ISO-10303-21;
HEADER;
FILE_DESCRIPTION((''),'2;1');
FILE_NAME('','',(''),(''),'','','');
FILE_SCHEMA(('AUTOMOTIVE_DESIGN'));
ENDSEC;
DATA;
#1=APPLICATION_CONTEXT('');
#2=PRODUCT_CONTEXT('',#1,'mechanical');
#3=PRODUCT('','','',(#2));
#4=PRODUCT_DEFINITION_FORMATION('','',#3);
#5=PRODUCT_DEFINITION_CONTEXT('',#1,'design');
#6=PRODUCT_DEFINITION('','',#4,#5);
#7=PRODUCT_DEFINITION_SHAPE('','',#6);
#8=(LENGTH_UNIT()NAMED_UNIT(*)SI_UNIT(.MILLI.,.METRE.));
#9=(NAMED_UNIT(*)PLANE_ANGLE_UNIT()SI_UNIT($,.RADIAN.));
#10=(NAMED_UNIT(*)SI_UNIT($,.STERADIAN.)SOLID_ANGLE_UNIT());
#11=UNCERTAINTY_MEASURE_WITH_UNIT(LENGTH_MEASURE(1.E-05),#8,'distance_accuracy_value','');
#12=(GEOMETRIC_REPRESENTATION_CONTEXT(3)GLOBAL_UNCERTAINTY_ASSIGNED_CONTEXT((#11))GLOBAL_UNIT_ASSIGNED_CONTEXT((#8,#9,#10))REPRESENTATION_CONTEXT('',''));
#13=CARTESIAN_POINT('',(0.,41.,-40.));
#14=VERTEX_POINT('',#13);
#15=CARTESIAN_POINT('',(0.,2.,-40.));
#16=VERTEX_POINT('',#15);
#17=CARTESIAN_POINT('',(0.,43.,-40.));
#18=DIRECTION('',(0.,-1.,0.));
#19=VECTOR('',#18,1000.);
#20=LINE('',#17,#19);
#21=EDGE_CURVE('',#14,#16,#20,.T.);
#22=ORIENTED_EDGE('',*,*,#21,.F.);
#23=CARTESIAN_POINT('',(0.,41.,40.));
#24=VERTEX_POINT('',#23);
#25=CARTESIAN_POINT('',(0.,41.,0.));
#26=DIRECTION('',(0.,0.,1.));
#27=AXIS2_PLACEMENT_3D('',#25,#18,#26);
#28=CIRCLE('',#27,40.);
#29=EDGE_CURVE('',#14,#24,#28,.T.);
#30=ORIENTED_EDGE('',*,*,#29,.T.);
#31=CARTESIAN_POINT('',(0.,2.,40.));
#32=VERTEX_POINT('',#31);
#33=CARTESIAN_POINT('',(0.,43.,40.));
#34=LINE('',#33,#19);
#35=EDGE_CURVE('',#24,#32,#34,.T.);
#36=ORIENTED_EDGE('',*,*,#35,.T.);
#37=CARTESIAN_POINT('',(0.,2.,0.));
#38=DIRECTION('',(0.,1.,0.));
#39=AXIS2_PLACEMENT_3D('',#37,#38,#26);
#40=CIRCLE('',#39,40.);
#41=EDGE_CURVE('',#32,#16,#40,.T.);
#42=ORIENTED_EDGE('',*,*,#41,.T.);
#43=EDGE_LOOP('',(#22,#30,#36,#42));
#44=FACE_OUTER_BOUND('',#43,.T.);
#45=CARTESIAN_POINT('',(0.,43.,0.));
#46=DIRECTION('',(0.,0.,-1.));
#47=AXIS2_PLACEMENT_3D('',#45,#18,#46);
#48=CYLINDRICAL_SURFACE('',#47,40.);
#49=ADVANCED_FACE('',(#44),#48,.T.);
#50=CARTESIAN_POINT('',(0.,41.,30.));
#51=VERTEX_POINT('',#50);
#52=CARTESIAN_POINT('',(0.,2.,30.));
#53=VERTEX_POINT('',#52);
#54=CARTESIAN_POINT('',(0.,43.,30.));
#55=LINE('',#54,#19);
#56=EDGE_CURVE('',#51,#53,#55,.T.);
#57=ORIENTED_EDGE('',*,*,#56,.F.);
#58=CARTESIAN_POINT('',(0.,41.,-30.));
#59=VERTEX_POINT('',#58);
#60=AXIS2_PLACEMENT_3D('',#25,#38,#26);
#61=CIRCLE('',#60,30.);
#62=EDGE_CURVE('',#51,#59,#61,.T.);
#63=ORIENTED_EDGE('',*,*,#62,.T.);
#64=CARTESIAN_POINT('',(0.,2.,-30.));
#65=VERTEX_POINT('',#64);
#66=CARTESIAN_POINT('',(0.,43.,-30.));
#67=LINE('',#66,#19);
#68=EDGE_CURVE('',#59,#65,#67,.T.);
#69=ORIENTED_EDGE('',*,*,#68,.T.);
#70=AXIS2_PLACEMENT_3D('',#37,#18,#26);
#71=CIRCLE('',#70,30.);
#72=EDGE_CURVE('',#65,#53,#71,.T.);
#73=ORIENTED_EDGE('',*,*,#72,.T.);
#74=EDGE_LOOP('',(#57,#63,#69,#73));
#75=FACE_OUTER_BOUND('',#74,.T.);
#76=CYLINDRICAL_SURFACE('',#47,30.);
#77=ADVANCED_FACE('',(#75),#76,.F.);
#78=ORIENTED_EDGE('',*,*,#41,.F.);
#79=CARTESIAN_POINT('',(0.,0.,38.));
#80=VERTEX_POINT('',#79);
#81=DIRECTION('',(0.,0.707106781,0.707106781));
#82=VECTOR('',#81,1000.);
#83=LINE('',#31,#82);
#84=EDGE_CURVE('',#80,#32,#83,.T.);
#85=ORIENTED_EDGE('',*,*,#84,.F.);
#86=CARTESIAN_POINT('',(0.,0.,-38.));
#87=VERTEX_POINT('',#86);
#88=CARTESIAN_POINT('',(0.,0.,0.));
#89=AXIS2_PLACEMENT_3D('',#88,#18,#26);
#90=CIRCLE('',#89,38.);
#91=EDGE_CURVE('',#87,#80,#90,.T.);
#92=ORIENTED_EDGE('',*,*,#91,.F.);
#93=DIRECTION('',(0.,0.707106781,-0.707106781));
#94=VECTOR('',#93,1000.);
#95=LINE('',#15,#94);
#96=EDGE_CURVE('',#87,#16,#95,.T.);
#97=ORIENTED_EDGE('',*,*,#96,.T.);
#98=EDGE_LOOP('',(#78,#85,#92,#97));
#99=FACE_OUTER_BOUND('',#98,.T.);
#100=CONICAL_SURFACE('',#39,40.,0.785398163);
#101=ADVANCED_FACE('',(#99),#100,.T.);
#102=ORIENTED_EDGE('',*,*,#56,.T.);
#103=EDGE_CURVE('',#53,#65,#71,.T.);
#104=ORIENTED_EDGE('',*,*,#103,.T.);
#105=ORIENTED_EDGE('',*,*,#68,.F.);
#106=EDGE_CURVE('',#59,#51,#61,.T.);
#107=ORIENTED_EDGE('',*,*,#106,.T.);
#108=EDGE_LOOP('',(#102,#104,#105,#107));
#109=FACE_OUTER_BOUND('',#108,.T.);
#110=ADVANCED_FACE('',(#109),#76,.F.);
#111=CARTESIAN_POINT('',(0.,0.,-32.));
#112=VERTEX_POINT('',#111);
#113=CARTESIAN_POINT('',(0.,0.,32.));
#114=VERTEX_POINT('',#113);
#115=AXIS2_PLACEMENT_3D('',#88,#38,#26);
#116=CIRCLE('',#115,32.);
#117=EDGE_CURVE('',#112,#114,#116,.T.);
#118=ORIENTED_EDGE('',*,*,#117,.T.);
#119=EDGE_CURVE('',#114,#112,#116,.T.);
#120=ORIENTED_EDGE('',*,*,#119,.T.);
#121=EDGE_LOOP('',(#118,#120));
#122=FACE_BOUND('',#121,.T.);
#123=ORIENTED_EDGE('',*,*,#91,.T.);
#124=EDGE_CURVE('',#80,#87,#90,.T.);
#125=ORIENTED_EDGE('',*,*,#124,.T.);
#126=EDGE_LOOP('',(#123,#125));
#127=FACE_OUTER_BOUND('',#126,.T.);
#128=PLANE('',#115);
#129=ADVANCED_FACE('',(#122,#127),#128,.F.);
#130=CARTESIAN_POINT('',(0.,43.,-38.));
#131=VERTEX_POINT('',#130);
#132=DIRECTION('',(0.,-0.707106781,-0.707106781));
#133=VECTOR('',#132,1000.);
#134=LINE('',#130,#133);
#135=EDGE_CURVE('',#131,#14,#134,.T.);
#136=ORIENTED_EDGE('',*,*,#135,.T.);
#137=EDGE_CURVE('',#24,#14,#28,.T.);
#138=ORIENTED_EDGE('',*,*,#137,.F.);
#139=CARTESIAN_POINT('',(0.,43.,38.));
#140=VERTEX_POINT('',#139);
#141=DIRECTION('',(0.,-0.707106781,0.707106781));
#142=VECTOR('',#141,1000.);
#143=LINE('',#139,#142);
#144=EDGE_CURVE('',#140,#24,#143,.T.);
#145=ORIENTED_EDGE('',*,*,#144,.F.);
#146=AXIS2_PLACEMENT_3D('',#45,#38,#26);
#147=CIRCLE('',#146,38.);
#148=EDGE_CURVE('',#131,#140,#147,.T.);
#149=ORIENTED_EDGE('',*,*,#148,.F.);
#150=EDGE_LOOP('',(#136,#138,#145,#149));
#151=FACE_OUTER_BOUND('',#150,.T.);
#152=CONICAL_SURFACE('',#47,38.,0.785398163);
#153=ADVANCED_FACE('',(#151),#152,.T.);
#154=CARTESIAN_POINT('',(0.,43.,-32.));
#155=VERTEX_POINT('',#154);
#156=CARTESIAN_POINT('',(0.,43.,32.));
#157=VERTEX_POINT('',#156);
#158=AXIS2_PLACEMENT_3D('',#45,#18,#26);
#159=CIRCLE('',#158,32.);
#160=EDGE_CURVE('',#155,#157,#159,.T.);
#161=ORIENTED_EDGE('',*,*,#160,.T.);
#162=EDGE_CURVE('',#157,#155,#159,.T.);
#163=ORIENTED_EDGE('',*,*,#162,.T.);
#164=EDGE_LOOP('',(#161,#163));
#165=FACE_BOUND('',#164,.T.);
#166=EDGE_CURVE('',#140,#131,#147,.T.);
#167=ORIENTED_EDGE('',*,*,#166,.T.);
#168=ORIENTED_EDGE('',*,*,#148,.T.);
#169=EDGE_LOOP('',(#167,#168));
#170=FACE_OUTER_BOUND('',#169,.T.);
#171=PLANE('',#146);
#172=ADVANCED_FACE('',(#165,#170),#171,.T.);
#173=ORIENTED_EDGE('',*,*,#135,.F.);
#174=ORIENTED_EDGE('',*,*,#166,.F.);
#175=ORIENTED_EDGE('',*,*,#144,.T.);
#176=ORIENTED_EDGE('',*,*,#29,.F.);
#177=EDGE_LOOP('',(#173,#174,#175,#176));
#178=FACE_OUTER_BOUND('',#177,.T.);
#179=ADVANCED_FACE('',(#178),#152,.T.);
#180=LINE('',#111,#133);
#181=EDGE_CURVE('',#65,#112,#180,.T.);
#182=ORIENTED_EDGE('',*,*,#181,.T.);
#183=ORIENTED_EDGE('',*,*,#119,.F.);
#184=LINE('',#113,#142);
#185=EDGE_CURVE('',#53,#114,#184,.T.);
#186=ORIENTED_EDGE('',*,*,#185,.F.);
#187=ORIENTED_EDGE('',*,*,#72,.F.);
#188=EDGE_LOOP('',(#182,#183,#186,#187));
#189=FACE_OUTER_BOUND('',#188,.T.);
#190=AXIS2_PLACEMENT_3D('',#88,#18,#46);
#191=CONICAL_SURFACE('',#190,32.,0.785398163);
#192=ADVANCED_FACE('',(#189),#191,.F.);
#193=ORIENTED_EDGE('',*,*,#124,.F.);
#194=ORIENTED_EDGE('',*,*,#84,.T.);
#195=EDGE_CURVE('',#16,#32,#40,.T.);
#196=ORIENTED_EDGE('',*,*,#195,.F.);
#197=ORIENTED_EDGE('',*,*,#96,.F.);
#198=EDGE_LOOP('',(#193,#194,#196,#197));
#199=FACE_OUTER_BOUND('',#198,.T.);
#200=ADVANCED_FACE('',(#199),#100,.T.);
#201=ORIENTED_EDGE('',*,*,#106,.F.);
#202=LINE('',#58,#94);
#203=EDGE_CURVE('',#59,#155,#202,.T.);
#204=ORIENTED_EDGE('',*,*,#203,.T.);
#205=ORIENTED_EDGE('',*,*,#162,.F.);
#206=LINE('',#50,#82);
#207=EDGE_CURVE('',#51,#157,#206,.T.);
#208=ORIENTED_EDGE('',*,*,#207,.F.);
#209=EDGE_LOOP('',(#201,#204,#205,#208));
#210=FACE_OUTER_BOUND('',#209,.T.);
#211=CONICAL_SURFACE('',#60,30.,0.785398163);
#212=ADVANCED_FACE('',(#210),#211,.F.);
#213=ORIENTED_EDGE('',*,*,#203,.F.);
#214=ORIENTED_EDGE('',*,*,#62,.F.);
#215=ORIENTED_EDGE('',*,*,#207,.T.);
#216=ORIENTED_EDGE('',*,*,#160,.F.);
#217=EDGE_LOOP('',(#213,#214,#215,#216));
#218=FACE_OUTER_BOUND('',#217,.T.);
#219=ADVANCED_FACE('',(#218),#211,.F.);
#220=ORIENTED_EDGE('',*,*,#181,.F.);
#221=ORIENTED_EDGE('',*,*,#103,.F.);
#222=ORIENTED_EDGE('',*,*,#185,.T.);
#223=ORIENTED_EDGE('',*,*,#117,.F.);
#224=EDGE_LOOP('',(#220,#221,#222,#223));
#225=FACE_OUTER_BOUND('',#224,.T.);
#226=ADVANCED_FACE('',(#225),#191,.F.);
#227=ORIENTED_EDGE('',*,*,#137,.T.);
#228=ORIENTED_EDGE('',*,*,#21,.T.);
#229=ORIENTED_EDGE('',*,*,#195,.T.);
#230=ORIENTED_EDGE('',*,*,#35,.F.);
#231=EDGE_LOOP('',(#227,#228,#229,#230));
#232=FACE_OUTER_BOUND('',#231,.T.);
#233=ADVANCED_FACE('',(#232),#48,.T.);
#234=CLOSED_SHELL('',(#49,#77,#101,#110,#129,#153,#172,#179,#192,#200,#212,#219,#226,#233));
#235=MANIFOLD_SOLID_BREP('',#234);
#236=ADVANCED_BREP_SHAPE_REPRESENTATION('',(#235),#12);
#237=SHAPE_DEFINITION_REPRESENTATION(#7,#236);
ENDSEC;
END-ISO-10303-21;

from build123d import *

# Parameters (mm, degrees)
SKETCH1_R           = 40
SKETCH1_R_2         = 30
BOSS_EXTRUDE1_DEPTH = 43
CHAMFER2_SIZE       = 2


with BuildPart() as part:
    # Sketch1 → Boss-Extrude1 (new body)
    with BuildSketch(Plane(origin=(0, 0, 0), x_dir=(1, 0, 0), z_dir=(0, 1, 0))):
        with Locations(Location((0, 0, 0), (0, 0, 270))):
            Circle(SKETCH1_R)
        with Locations(Location((0, 0, 0), (0, 0, 270))):
            Circle(SKETCH1_R_2, mode=Mode.SUBTRACT)
    extrude(amount=BOSS_EXTRUDE1_DEPTH)

    # Chamfer2
    chamfer2_edges = [part.edges().sort_by_distance(p)[0] for p in [
        (0, 0, -40),
        (0, 43, -40),
        (0, 0, -30),
        (0, 43, -30),
    ]]
    chamfer(chamfer2_edges, length=CHAMFER2_SIZE)


solid = part.part
